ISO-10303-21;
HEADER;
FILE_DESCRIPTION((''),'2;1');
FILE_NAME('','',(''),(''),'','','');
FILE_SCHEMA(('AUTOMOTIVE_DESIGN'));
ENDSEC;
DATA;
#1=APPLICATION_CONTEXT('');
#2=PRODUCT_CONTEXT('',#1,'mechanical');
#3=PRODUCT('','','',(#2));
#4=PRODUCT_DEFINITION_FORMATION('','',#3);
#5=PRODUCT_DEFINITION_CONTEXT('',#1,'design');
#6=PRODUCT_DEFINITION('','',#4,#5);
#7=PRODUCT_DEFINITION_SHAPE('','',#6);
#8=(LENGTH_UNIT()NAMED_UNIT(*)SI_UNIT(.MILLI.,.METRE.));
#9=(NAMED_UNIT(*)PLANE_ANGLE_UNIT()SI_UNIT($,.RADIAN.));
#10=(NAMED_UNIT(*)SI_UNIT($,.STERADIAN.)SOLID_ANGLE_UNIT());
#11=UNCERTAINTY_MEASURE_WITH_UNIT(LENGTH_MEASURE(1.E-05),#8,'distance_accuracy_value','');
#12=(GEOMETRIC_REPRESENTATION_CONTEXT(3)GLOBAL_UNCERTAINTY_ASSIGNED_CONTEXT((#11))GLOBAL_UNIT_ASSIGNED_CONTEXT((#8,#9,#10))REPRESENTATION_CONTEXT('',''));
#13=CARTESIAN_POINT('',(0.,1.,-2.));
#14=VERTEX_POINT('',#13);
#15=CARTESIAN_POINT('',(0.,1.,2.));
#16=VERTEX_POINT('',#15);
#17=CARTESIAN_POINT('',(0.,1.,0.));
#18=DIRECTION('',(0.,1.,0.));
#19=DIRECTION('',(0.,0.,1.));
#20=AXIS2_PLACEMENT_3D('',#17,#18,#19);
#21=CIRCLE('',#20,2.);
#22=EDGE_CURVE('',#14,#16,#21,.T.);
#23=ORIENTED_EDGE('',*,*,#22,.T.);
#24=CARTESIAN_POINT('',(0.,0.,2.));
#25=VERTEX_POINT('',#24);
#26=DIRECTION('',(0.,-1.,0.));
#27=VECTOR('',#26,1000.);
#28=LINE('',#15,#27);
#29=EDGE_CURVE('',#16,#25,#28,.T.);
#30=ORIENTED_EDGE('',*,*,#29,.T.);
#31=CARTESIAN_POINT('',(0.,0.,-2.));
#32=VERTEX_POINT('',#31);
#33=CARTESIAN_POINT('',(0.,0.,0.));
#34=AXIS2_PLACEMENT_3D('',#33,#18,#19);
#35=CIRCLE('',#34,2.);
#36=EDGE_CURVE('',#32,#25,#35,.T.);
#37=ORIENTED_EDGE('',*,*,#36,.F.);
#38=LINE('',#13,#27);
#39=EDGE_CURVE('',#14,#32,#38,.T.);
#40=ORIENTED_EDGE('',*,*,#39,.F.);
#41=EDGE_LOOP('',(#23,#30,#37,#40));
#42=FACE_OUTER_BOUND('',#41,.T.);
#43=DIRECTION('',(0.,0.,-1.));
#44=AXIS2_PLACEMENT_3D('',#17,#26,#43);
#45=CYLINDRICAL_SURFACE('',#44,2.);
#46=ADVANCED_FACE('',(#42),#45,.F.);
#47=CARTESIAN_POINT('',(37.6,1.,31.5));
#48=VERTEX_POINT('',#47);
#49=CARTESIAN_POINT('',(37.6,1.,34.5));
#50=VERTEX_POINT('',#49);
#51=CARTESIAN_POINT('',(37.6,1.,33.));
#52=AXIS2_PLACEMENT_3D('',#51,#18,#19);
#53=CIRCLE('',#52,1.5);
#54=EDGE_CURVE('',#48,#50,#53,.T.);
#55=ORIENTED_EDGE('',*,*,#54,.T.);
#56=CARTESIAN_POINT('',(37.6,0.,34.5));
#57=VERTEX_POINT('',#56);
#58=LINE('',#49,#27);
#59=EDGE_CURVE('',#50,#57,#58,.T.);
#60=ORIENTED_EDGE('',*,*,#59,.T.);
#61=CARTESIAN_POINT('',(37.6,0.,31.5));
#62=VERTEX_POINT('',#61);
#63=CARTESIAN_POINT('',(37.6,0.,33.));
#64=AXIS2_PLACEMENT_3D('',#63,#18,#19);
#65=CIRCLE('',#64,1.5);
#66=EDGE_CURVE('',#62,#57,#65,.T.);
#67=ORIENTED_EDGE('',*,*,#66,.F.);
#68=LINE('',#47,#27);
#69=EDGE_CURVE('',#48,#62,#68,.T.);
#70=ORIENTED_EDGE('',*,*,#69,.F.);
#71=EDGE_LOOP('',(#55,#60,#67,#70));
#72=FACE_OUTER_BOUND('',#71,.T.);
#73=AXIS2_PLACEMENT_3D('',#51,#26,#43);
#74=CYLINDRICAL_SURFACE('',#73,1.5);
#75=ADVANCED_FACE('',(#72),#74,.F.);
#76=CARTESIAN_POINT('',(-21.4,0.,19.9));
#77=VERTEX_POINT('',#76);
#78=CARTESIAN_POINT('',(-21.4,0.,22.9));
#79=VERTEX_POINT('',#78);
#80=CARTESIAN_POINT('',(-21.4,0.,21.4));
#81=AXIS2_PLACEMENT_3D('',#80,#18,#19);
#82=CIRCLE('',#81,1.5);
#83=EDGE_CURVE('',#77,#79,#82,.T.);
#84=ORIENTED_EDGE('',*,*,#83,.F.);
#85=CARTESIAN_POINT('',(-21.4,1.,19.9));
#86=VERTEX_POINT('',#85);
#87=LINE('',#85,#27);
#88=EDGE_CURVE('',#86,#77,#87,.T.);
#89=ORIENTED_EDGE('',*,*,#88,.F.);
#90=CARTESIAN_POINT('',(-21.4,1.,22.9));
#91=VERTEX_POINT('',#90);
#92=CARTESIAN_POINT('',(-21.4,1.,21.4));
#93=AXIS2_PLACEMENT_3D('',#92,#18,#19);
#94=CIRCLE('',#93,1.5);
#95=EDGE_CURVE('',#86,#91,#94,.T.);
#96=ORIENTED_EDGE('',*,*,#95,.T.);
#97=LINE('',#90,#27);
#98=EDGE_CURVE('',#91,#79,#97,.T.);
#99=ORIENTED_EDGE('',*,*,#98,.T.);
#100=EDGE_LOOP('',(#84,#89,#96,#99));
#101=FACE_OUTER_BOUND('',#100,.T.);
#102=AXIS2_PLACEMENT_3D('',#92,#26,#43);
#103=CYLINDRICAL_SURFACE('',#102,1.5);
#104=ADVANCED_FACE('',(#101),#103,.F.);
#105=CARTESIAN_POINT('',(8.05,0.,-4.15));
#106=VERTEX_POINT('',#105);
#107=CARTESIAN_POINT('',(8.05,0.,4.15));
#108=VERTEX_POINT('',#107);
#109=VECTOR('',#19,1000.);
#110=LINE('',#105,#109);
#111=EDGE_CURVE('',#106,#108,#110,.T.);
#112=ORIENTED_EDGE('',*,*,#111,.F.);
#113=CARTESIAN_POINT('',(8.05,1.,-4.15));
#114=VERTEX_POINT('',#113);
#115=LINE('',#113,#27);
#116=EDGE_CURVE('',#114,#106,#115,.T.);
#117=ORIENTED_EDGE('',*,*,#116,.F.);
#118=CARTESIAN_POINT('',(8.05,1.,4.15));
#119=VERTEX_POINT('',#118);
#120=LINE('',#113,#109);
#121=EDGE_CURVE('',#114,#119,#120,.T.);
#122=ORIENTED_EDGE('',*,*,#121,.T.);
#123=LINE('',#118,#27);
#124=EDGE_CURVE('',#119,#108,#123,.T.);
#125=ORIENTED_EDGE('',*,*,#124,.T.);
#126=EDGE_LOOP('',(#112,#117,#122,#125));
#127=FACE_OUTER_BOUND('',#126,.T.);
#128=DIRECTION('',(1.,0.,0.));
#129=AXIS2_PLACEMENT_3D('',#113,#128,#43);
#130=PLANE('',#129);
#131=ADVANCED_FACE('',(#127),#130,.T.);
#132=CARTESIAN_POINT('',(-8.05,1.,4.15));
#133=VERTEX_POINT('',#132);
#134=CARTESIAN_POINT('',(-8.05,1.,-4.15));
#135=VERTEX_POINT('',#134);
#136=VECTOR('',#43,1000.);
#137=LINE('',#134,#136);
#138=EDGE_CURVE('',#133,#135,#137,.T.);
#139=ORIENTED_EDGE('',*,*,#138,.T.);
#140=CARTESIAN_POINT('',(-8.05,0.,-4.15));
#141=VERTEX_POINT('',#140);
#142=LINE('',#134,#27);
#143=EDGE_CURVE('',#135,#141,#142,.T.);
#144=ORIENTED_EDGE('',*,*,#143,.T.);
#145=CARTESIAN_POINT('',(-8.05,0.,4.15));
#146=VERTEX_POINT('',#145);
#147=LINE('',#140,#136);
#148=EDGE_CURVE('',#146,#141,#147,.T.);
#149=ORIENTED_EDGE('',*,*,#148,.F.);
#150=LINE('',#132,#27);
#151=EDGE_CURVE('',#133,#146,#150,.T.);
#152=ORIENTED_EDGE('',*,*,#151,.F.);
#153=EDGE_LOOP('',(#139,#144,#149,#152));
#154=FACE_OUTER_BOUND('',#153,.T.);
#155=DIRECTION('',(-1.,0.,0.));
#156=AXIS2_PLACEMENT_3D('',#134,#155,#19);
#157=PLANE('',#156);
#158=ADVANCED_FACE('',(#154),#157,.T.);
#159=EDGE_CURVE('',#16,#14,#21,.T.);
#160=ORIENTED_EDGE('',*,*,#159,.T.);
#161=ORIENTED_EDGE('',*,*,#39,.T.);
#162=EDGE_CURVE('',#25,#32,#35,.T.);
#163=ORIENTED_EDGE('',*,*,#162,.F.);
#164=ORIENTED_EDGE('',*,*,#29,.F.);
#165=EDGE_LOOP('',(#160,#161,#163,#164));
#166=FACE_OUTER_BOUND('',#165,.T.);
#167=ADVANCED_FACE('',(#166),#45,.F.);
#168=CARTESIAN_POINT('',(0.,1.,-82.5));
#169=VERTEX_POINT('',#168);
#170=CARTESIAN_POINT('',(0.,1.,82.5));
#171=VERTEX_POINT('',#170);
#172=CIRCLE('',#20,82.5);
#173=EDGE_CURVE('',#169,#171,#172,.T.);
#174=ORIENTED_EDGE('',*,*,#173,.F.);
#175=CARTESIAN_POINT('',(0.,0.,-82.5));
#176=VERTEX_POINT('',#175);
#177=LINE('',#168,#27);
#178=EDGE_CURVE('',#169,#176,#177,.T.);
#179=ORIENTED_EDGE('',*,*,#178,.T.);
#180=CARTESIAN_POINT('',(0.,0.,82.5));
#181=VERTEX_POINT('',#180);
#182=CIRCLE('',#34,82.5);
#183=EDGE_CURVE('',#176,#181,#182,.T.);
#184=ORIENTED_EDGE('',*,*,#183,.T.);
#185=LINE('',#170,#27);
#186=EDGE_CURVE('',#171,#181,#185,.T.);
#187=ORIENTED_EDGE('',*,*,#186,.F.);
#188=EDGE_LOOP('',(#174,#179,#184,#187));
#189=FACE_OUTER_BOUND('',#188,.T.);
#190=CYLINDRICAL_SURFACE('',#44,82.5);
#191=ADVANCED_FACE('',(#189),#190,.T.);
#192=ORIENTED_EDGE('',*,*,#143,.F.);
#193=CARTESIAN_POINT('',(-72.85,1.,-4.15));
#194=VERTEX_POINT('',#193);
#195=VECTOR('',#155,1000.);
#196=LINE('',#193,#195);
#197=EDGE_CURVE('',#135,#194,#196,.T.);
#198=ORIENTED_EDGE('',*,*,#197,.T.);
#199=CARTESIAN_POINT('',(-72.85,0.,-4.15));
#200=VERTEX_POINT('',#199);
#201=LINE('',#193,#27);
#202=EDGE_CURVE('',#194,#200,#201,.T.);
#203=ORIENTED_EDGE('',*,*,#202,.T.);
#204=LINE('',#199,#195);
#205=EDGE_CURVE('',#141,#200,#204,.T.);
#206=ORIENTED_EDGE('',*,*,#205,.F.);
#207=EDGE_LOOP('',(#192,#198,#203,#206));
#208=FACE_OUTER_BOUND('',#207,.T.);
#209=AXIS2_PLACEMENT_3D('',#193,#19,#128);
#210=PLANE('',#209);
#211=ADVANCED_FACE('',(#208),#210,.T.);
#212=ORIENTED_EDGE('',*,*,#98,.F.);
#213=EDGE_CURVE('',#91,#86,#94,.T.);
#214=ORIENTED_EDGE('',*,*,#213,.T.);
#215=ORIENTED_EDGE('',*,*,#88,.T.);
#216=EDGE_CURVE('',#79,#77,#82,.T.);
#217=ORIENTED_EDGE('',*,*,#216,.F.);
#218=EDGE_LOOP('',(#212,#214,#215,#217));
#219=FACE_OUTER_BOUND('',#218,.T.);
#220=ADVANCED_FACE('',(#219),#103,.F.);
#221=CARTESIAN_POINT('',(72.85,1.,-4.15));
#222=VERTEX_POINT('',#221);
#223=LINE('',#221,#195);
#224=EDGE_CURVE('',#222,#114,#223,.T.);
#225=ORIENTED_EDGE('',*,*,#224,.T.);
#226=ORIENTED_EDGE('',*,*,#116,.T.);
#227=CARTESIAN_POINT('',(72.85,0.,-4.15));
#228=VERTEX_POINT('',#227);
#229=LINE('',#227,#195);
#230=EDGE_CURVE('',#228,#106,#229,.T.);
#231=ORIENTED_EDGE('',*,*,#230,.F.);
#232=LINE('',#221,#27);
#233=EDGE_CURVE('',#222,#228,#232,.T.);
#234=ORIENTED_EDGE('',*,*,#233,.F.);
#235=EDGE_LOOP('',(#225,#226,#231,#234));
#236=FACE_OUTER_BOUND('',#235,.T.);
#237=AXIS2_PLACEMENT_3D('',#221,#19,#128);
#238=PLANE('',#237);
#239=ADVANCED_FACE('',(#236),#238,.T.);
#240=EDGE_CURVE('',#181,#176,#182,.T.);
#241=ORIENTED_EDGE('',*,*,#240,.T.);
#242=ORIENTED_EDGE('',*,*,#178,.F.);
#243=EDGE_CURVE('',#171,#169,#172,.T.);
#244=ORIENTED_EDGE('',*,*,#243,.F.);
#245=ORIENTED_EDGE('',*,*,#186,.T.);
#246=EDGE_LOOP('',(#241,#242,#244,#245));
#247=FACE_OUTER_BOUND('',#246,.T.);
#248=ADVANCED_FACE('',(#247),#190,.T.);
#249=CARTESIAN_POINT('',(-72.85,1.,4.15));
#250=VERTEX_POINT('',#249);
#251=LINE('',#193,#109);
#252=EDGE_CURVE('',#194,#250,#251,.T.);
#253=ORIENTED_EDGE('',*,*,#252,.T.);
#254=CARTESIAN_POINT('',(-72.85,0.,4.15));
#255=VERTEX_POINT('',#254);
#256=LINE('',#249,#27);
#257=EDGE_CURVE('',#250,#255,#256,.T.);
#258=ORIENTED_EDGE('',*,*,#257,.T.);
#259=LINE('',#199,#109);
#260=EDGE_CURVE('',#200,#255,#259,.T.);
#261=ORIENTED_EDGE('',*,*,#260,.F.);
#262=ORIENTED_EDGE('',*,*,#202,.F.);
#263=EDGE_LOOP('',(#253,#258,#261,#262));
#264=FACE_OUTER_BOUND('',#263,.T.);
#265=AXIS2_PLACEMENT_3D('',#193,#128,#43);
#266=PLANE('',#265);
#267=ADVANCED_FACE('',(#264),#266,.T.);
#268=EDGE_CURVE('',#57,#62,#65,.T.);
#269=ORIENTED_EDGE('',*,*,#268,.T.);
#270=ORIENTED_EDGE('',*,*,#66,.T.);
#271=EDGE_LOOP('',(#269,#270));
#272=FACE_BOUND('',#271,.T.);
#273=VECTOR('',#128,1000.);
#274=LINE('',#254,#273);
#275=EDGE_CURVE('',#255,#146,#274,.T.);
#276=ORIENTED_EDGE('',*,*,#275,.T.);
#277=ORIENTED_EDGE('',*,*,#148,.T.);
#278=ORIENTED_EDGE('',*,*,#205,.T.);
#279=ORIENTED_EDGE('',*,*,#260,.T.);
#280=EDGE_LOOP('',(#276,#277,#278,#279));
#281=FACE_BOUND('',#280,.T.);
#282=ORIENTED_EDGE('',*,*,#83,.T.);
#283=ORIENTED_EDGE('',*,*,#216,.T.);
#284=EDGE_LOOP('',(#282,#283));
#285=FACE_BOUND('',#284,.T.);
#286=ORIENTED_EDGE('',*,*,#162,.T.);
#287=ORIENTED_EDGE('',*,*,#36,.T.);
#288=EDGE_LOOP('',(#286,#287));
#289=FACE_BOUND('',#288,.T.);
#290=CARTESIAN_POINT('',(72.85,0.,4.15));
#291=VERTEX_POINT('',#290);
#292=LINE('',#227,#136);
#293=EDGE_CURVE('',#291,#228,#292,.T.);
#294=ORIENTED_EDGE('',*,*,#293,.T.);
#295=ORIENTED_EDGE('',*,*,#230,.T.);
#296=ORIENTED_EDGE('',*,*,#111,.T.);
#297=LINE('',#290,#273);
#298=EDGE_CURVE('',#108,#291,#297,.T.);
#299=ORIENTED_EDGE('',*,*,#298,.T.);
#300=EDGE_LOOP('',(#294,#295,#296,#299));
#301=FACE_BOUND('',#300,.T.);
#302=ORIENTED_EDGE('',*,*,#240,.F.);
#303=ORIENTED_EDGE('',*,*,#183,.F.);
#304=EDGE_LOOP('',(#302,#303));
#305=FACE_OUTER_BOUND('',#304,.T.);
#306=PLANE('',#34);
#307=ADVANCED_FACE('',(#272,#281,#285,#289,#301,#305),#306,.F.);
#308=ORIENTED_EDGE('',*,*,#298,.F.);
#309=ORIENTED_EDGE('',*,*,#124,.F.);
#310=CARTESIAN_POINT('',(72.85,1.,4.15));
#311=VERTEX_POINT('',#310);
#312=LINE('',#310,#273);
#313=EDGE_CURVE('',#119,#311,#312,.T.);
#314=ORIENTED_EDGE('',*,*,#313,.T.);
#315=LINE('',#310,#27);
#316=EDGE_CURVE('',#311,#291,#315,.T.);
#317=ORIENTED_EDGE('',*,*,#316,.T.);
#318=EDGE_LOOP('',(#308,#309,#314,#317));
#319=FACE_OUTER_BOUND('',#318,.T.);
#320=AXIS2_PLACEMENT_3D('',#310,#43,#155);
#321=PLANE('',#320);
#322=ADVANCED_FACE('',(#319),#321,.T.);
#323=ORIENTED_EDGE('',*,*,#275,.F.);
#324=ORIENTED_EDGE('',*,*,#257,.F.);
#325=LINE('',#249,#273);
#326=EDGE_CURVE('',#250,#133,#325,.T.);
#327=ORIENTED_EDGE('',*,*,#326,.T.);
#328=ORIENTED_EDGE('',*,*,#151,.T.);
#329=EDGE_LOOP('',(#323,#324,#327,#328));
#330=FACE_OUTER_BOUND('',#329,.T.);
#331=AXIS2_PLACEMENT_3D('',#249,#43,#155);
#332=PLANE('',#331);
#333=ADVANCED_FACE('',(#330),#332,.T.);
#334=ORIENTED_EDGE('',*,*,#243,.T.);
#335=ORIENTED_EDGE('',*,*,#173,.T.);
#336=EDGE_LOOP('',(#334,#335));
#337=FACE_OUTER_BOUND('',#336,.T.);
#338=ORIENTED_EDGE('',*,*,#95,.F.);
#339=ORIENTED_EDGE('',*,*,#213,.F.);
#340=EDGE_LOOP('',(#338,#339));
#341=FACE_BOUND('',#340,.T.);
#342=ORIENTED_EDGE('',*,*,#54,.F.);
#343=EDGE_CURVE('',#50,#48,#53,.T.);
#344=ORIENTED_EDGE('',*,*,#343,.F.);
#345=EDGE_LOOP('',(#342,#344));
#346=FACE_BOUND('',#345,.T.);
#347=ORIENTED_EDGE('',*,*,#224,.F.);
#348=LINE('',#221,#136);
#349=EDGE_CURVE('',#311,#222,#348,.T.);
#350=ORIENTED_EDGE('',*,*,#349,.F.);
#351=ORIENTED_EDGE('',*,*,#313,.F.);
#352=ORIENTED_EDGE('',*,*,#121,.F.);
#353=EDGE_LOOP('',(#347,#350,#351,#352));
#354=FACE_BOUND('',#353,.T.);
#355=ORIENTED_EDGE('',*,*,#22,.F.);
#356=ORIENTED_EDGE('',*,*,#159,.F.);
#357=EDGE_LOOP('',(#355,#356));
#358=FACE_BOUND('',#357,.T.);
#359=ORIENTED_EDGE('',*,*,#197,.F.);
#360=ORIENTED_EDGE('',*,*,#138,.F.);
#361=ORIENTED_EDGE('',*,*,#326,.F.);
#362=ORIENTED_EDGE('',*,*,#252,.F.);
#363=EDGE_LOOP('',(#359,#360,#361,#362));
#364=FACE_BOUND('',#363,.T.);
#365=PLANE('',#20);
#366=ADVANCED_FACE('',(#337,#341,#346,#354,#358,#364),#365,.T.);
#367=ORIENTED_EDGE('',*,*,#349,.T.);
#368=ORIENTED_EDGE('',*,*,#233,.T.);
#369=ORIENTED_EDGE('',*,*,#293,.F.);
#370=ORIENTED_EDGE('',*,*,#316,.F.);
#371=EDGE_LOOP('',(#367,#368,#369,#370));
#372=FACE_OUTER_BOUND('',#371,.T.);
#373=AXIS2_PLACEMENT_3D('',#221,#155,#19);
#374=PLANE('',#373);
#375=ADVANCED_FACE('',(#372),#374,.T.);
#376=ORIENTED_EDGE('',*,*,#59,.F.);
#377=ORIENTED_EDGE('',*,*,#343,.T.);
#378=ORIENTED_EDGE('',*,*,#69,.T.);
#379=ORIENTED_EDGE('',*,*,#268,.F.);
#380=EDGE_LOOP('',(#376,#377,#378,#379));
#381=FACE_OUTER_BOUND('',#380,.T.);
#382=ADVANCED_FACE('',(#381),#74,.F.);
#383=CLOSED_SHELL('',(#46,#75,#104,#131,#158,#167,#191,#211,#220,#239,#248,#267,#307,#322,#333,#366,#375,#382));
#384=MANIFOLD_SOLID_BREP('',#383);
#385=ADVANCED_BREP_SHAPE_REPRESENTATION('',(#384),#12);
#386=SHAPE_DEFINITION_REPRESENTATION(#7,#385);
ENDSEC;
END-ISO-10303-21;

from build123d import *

# Parameters (mm, degrees)
SKETCH1_R           = 82.5
SKETCH1_R_2         = 1.5
SKETCH1_R_3         = 2
SKETCH1_W           = 64.8
SKETCH1_H           = 8.3
BOSS_EXTRUDE1_DEPTH = 1


with BuildPart() as part:
    # Sketch1 → Boss-Extrude1 (new body)
    with BuildSketch(Plane(origin=(0, 0, 0), x_dir=(1, 0, 0), z_dir=(0, 1, 0))):
        with Locations(Location((0, 0, 0), (0, 0, 270))):
            Circle(SKETCH1_R)
        with Locations(Location((-21.4, -21.4, 0), (0, 0, 270))):
            Circle(SKETCH1_R_2, mode=Mode.SUBTRACT)
        with Locations(Location((37.6, -33, 0), (0, 0, 270))):
            Circle(SKETCH1_R_2, mode=Mode.SUBTRACT)
        with Locations(Location((0, 0, 0), (0, 0, 270))):
            Circle(SKETCH1_R_3, mode=Mode.SUBTRACT)
        with Locations((-40.45, 0)):
            Rectangle(SKETCH1_W, SKETCH1_H, mode=Mode.SUBTRACT)
        with Locations((40.45, 0)):
            Rectangle(SKETCH1_W, SKETCH1_H, mode=Mode.SUBTRACT)
    extrude(amount=BOSS_EXTRUDE1_DEPTH)


solid = part.part
